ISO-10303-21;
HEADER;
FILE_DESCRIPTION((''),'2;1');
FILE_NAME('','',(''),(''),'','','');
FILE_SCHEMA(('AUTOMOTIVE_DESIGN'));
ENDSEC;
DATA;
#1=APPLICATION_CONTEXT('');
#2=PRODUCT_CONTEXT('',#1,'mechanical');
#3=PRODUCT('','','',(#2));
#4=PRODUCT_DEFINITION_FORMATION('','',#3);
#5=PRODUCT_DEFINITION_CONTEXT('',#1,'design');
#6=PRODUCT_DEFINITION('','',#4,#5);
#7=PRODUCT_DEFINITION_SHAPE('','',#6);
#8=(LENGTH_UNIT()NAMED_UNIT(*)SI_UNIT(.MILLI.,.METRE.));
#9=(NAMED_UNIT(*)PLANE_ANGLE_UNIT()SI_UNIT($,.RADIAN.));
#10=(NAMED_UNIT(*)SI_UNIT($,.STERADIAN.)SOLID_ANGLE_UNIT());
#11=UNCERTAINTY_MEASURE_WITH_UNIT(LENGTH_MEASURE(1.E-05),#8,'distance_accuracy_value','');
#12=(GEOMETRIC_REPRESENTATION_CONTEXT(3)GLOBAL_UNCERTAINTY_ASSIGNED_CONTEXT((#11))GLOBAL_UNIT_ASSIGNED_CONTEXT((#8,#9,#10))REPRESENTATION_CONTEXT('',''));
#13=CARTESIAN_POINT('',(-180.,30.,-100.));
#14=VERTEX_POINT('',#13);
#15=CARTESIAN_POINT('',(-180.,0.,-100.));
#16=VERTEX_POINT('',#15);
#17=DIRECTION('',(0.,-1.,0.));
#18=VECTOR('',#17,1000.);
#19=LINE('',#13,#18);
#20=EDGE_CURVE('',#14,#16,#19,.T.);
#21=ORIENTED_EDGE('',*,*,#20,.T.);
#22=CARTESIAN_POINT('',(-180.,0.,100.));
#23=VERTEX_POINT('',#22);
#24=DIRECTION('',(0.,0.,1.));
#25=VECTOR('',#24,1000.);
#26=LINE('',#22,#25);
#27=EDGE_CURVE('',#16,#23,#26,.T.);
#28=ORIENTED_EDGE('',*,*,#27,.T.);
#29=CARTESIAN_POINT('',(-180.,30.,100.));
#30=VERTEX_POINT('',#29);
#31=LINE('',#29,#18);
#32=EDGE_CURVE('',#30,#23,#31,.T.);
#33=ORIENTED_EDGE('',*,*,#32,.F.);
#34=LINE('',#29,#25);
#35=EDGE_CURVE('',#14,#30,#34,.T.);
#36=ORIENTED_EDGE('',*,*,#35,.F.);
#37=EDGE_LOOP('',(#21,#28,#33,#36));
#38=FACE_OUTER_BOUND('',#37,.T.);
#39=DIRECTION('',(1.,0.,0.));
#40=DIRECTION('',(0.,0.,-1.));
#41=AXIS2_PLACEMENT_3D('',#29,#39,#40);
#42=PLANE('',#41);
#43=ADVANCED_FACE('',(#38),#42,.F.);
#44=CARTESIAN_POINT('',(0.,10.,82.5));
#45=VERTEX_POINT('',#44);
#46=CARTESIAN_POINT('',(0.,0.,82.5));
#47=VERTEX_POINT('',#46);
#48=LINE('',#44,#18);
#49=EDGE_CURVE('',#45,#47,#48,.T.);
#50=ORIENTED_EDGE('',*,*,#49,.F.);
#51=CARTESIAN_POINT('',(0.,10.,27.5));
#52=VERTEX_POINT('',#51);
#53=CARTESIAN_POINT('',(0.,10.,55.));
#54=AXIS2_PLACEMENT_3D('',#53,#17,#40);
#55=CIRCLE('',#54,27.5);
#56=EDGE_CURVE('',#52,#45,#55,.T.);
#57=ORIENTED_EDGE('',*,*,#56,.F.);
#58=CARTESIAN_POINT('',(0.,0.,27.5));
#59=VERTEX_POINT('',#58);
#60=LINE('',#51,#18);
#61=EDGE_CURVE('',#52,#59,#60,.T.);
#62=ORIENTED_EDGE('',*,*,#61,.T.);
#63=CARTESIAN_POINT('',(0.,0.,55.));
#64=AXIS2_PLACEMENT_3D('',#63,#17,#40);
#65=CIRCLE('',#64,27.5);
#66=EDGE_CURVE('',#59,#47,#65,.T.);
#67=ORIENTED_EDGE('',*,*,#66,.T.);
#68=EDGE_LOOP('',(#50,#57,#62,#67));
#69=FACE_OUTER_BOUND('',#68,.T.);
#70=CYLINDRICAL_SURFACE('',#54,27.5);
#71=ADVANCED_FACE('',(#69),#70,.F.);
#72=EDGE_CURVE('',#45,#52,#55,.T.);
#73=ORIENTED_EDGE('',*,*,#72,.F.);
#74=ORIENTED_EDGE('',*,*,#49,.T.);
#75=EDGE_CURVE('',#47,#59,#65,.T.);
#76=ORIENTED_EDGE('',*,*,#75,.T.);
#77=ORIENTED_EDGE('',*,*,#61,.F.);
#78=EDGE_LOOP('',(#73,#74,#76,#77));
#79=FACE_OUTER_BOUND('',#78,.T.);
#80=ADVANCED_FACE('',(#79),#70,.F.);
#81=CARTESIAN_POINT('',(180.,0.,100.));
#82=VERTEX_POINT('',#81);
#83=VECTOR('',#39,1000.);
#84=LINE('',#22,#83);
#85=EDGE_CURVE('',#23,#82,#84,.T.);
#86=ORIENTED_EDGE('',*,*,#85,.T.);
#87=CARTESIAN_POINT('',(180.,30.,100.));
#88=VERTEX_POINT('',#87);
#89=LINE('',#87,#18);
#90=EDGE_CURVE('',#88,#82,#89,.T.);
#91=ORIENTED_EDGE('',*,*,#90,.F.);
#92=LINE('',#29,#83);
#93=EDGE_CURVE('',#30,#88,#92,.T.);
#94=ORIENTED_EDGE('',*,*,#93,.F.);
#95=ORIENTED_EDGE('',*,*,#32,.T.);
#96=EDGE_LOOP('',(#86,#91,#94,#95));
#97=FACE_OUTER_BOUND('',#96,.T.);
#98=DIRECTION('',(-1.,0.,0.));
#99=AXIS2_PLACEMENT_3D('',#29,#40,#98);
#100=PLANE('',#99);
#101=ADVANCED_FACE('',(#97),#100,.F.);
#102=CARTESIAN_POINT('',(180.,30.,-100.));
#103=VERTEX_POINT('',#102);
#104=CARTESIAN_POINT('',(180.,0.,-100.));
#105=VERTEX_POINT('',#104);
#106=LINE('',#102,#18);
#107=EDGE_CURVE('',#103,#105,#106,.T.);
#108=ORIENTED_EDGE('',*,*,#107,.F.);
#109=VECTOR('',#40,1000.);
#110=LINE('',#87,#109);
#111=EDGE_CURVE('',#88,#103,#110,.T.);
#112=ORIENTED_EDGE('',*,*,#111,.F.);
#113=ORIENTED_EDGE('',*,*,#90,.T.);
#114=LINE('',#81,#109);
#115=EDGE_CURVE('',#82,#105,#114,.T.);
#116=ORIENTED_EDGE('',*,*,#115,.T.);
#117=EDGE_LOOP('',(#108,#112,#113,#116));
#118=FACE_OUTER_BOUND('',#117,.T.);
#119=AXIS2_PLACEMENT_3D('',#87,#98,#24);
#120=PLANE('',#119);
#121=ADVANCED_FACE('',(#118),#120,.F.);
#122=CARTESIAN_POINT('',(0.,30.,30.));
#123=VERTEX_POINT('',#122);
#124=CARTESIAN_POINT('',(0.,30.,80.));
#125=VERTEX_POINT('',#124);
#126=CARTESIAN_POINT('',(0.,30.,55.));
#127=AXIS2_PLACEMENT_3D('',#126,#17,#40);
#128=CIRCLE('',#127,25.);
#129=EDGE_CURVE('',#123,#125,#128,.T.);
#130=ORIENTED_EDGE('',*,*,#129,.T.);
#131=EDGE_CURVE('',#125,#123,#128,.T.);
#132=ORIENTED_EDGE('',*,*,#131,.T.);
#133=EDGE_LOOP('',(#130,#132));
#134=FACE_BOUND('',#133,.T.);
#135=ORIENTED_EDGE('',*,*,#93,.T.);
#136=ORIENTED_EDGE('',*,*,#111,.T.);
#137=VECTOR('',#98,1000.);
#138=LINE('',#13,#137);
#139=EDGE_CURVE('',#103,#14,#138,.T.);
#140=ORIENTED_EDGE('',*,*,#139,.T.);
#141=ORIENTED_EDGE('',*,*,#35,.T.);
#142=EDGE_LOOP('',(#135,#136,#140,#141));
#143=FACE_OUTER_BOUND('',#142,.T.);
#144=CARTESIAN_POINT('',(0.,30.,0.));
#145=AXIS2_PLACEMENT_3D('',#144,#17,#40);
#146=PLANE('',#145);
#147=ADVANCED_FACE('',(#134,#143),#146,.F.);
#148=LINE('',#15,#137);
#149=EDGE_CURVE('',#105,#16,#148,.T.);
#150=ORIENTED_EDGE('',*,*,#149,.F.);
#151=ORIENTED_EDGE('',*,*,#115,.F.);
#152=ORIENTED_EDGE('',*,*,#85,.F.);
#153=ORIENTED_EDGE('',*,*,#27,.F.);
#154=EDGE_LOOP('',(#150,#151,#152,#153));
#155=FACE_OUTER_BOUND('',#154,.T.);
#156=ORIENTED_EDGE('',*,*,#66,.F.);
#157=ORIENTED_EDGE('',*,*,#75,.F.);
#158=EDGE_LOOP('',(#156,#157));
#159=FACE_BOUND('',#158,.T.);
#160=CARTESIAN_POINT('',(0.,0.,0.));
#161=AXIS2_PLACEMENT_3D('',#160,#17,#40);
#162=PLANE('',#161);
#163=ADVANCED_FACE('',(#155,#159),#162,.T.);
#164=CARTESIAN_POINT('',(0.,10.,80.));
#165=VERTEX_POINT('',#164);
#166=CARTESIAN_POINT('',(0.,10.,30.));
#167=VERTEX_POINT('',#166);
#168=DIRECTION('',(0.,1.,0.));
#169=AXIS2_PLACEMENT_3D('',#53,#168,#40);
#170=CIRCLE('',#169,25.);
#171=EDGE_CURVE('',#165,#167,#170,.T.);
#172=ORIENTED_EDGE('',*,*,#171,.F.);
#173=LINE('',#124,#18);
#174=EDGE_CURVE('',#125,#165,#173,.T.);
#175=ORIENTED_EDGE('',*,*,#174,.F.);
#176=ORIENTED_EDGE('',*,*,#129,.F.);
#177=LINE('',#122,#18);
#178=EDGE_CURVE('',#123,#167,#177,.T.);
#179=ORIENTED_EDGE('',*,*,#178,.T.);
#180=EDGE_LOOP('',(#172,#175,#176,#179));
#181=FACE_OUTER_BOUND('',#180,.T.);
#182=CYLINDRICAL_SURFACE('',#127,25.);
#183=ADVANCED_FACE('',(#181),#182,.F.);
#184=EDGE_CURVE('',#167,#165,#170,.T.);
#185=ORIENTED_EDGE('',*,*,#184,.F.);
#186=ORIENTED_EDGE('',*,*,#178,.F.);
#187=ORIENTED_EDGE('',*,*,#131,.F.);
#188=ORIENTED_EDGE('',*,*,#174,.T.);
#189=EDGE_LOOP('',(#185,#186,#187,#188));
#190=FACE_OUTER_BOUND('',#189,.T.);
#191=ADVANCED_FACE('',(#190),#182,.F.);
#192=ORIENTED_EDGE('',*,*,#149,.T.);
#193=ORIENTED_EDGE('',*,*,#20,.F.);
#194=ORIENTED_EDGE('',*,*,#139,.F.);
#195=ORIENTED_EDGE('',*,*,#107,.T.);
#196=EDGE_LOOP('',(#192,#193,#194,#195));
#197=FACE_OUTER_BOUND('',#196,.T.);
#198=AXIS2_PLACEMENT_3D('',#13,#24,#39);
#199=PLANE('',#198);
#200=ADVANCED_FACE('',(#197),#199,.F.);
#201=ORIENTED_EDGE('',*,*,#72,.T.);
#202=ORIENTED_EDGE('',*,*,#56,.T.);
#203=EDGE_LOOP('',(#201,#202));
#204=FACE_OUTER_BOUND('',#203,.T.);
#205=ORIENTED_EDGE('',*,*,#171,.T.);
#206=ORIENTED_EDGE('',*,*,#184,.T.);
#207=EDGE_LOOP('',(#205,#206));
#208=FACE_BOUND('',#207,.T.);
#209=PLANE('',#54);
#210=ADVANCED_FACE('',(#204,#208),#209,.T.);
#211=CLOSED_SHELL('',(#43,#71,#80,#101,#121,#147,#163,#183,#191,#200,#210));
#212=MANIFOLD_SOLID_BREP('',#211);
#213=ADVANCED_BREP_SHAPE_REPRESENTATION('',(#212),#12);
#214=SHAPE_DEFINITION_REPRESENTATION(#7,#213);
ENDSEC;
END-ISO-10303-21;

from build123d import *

# Parameters (mm, degrees)
SKETCH_1_W          = 360
SKETCH_1_H          = 200
EXTRUDE_1_DEPTH     = 30
SKETCH_2_R          = 25
CUT_EXTRUDE_1_DEPTH = 209.086520467
SKETCH_3_R          = 27.5
CUT_EXTRUDE_2_DEPTH = 10


with BuildPart() as part:
    # 草图1 → 凸台-拉伸1 (new body)
    with BuildSketch(Plane(origin=(0, 0, 0), x_dir=(1, 0, 0), z_dir=(0, 1, 0))):
        Rectangle(SKETCH_1_W, SKETCH_1_H)
    extrude(amount=EXTRUDE_1_DEPTH)

    # 草图2 → 切除-拉伸1 (cut, through all)
    with BuildSketch(Plane.XZ):
        with Locations(Location((0, 55, 0), (0, 0, 270))):
            Circle(SKETCH_2_R)
    extrude(amount=-CUT_EXTRUDE_1_DEPTH, mode=Mode.SUBTRACT)

    # 草图3 → 切除-拉伸2 (cut)
    with BuildSketch(Plane.XZ):
        with Locations(Location((0, 55, 0), (0, 0, 270))):
            Circle(SKETCH_3_R)
    extrude(amount=-CUT_EXTRUDE_2_DEPTH, mode=Mode.SUBTRACT)


solid = part.part
